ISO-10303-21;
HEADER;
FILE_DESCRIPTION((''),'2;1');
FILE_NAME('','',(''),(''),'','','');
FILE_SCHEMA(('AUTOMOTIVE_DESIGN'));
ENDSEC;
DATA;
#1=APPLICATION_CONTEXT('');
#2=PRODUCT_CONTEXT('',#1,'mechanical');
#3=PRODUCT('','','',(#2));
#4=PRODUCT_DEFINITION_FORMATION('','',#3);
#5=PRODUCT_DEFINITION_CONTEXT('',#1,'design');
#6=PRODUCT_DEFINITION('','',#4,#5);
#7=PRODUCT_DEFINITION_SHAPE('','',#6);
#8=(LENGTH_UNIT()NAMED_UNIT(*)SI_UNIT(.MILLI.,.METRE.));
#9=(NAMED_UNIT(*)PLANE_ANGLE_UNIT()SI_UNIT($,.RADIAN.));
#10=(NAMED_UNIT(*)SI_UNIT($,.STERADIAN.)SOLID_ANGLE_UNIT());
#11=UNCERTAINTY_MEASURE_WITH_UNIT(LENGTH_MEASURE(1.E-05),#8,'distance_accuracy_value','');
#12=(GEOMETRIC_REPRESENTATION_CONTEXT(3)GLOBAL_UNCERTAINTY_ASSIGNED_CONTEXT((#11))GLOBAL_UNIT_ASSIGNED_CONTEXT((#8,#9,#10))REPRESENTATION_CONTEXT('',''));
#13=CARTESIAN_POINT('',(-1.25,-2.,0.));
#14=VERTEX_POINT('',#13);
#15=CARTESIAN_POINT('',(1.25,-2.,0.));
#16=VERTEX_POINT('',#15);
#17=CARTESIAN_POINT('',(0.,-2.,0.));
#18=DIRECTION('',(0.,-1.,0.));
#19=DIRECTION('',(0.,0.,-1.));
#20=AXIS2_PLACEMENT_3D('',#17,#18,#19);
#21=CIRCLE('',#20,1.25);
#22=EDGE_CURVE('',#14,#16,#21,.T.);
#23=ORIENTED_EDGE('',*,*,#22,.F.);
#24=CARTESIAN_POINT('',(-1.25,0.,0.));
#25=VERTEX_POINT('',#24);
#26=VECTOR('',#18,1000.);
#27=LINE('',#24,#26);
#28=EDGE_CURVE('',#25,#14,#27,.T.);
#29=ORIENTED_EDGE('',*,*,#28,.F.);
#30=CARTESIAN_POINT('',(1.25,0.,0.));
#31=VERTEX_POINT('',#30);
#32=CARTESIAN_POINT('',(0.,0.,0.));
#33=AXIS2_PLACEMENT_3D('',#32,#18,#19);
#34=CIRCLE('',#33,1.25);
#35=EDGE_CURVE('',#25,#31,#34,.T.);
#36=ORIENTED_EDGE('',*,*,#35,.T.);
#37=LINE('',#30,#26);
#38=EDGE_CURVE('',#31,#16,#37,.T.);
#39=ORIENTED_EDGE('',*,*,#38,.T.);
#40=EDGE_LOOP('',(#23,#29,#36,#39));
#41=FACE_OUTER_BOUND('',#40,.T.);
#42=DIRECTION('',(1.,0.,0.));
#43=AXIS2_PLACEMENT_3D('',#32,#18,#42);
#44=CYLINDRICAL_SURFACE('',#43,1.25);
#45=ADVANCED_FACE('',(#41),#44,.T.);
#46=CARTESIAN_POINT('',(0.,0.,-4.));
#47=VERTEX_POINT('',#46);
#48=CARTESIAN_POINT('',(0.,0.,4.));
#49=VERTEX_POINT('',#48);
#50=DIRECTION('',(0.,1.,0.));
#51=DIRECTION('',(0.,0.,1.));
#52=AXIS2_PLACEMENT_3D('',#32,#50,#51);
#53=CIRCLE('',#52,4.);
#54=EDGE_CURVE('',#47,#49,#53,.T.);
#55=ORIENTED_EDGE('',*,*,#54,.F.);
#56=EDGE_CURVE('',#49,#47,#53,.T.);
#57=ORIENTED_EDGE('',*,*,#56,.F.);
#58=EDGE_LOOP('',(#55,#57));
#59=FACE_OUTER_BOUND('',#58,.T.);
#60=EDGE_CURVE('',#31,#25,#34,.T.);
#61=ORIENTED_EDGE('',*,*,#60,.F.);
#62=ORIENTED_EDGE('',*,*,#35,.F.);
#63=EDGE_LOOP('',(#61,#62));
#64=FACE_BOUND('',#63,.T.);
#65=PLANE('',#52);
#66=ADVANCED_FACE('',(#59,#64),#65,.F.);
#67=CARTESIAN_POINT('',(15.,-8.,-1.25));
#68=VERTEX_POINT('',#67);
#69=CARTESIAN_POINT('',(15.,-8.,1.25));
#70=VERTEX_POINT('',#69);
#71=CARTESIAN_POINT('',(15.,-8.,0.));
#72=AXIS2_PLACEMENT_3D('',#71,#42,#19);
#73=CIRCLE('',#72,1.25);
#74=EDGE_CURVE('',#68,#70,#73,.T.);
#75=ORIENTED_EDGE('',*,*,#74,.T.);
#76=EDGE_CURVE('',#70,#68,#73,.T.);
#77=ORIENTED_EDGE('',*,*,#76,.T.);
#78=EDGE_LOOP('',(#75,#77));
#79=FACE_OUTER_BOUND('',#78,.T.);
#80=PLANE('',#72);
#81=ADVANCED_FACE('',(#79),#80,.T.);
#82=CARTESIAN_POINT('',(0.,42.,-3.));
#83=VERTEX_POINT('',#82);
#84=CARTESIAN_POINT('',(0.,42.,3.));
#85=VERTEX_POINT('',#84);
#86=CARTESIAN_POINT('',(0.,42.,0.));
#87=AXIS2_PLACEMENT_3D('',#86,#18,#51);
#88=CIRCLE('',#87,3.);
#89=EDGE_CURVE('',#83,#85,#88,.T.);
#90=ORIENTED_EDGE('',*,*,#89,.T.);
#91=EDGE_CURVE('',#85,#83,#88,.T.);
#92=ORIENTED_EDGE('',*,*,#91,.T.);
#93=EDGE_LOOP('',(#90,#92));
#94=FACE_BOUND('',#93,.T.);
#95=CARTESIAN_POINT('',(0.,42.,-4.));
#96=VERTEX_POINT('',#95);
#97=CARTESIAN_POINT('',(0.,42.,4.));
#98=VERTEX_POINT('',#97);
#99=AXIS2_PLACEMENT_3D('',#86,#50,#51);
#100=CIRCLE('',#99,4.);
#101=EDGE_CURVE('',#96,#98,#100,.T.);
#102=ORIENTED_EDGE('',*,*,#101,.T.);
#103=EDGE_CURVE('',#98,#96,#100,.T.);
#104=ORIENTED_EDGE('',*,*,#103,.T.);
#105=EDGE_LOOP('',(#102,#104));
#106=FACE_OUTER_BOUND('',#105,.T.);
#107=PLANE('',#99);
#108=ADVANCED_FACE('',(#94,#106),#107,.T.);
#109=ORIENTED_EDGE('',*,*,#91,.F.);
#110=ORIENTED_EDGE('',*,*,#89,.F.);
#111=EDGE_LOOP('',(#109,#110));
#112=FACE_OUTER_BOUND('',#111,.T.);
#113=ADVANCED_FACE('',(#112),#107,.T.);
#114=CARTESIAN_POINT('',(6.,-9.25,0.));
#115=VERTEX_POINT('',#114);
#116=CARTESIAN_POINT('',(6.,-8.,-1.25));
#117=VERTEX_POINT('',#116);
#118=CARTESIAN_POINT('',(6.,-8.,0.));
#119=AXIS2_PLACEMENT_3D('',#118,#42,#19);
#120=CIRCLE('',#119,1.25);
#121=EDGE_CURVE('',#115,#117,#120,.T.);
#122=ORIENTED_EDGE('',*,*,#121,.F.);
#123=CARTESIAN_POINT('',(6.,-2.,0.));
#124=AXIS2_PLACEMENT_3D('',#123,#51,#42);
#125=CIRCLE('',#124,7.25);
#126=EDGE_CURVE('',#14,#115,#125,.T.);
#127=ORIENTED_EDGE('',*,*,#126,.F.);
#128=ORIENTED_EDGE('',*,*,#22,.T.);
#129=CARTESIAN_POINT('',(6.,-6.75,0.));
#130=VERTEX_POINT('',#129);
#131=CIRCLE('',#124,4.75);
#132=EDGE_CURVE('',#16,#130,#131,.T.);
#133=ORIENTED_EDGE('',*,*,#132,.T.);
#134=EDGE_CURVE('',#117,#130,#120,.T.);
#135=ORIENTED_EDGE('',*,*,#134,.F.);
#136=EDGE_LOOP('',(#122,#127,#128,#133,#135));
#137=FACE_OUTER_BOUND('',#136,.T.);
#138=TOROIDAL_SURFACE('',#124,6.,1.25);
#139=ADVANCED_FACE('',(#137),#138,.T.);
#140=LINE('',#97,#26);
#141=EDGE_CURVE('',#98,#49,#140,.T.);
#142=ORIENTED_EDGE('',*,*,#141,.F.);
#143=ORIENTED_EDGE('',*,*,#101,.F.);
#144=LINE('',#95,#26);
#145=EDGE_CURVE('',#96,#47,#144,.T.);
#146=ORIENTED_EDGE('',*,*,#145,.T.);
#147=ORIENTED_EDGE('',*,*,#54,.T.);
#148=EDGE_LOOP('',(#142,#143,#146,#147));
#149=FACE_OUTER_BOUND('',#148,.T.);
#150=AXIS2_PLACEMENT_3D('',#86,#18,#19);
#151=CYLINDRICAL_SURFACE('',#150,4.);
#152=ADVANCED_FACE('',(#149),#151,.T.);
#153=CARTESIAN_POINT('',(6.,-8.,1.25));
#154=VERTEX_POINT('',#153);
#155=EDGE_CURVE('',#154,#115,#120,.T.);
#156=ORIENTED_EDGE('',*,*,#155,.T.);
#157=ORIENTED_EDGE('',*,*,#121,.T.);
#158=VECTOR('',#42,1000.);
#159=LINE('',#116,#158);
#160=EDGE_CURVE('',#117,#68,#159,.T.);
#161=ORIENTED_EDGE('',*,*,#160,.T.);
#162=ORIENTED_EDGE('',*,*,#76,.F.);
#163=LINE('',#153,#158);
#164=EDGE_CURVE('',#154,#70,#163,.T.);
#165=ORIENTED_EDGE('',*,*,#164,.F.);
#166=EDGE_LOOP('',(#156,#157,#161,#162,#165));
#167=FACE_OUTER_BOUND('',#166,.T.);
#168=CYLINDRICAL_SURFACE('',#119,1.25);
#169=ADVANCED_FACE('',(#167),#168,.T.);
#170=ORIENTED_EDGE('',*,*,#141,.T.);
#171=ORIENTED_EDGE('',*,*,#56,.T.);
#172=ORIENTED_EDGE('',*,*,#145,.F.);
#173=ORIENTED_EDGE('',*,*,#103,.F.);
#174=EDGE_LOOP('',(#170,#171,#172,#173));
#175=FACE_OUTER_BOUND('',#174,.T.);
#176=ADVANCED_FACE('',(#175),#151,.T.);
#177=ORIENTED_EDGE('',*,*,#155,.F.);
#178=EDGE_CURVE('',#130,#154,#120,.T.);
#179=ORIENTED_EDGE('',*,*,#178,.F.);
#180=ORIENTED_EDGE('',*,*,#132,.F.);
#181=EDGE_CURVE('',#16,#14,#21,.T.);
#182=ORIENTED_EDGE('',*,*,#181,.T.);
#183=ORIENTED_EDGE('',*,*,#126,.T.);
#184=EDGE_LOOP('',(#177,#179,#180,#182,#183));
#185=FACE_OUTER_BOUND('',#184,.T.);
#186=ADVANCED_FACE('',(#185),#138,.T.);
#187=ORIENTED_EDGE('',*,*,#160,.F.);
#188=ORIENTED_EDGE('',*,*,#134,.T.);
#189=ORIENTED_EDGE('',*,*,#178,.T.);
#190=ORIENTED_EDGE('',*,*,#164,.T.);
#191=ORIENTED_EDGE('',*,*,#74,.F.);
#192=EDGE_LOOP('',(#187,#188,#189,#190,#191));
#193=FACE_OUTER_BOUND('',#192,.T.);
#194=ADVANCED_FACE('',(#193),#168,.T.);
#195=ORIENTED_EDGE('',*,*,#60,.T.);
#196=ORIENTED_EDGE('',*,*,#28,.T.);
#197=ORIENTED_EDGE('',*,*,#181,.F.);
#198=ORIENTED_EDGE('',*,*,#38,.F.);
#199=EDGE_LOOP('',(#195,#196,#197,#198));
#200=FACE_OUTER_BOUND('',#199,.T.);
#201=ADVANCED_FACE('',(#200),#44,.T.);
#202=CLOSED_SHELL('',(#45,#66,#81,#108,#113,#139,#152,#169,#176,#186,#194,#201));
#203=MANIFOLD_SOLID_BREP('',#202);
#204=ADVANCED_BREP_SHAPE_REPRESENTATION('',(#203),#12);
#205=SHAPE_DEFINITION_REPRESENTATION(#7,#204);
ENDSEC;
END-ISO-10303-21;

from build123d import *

# Parameters (mm, degrees)
SKETCH1_R           = 4
BOSS_EXTRUDE1_DEPTH = 42
SKETCH2_R           = 1.25


with BuildPart() as part:
    # Sketch1 → Boss-Extrude1 (new body)
    with BuildSketch(Plane(origin=(0, 0, 0), x_dir=(1, 0, 0), z_dir=(0, 1, 0))):
        with Locations(Location((0, 0, 0), (0, 0, 90))):
            Circle(SKETCH1_R)
    extrude(amount=BOSS_EXTRUDE1_DEPTH)

    # Sweep1: sweep along a path in Sketch3
    with BuildLine(Plane.XY) as sweep1_path:
        Line((0, 0), (0, -2))
        ThreePointArc((0, -2), (1.757359313, -6.242640687), (6, -8))
        Line((6, -8), (15, -8))
    # Sketch2 → Sweep1 (sweep)
    with BuildSketch(Plane.XZ):
        Circle(SKETCH2_R)
    sweep(path=sweep1_path.line)


solid = part.part
